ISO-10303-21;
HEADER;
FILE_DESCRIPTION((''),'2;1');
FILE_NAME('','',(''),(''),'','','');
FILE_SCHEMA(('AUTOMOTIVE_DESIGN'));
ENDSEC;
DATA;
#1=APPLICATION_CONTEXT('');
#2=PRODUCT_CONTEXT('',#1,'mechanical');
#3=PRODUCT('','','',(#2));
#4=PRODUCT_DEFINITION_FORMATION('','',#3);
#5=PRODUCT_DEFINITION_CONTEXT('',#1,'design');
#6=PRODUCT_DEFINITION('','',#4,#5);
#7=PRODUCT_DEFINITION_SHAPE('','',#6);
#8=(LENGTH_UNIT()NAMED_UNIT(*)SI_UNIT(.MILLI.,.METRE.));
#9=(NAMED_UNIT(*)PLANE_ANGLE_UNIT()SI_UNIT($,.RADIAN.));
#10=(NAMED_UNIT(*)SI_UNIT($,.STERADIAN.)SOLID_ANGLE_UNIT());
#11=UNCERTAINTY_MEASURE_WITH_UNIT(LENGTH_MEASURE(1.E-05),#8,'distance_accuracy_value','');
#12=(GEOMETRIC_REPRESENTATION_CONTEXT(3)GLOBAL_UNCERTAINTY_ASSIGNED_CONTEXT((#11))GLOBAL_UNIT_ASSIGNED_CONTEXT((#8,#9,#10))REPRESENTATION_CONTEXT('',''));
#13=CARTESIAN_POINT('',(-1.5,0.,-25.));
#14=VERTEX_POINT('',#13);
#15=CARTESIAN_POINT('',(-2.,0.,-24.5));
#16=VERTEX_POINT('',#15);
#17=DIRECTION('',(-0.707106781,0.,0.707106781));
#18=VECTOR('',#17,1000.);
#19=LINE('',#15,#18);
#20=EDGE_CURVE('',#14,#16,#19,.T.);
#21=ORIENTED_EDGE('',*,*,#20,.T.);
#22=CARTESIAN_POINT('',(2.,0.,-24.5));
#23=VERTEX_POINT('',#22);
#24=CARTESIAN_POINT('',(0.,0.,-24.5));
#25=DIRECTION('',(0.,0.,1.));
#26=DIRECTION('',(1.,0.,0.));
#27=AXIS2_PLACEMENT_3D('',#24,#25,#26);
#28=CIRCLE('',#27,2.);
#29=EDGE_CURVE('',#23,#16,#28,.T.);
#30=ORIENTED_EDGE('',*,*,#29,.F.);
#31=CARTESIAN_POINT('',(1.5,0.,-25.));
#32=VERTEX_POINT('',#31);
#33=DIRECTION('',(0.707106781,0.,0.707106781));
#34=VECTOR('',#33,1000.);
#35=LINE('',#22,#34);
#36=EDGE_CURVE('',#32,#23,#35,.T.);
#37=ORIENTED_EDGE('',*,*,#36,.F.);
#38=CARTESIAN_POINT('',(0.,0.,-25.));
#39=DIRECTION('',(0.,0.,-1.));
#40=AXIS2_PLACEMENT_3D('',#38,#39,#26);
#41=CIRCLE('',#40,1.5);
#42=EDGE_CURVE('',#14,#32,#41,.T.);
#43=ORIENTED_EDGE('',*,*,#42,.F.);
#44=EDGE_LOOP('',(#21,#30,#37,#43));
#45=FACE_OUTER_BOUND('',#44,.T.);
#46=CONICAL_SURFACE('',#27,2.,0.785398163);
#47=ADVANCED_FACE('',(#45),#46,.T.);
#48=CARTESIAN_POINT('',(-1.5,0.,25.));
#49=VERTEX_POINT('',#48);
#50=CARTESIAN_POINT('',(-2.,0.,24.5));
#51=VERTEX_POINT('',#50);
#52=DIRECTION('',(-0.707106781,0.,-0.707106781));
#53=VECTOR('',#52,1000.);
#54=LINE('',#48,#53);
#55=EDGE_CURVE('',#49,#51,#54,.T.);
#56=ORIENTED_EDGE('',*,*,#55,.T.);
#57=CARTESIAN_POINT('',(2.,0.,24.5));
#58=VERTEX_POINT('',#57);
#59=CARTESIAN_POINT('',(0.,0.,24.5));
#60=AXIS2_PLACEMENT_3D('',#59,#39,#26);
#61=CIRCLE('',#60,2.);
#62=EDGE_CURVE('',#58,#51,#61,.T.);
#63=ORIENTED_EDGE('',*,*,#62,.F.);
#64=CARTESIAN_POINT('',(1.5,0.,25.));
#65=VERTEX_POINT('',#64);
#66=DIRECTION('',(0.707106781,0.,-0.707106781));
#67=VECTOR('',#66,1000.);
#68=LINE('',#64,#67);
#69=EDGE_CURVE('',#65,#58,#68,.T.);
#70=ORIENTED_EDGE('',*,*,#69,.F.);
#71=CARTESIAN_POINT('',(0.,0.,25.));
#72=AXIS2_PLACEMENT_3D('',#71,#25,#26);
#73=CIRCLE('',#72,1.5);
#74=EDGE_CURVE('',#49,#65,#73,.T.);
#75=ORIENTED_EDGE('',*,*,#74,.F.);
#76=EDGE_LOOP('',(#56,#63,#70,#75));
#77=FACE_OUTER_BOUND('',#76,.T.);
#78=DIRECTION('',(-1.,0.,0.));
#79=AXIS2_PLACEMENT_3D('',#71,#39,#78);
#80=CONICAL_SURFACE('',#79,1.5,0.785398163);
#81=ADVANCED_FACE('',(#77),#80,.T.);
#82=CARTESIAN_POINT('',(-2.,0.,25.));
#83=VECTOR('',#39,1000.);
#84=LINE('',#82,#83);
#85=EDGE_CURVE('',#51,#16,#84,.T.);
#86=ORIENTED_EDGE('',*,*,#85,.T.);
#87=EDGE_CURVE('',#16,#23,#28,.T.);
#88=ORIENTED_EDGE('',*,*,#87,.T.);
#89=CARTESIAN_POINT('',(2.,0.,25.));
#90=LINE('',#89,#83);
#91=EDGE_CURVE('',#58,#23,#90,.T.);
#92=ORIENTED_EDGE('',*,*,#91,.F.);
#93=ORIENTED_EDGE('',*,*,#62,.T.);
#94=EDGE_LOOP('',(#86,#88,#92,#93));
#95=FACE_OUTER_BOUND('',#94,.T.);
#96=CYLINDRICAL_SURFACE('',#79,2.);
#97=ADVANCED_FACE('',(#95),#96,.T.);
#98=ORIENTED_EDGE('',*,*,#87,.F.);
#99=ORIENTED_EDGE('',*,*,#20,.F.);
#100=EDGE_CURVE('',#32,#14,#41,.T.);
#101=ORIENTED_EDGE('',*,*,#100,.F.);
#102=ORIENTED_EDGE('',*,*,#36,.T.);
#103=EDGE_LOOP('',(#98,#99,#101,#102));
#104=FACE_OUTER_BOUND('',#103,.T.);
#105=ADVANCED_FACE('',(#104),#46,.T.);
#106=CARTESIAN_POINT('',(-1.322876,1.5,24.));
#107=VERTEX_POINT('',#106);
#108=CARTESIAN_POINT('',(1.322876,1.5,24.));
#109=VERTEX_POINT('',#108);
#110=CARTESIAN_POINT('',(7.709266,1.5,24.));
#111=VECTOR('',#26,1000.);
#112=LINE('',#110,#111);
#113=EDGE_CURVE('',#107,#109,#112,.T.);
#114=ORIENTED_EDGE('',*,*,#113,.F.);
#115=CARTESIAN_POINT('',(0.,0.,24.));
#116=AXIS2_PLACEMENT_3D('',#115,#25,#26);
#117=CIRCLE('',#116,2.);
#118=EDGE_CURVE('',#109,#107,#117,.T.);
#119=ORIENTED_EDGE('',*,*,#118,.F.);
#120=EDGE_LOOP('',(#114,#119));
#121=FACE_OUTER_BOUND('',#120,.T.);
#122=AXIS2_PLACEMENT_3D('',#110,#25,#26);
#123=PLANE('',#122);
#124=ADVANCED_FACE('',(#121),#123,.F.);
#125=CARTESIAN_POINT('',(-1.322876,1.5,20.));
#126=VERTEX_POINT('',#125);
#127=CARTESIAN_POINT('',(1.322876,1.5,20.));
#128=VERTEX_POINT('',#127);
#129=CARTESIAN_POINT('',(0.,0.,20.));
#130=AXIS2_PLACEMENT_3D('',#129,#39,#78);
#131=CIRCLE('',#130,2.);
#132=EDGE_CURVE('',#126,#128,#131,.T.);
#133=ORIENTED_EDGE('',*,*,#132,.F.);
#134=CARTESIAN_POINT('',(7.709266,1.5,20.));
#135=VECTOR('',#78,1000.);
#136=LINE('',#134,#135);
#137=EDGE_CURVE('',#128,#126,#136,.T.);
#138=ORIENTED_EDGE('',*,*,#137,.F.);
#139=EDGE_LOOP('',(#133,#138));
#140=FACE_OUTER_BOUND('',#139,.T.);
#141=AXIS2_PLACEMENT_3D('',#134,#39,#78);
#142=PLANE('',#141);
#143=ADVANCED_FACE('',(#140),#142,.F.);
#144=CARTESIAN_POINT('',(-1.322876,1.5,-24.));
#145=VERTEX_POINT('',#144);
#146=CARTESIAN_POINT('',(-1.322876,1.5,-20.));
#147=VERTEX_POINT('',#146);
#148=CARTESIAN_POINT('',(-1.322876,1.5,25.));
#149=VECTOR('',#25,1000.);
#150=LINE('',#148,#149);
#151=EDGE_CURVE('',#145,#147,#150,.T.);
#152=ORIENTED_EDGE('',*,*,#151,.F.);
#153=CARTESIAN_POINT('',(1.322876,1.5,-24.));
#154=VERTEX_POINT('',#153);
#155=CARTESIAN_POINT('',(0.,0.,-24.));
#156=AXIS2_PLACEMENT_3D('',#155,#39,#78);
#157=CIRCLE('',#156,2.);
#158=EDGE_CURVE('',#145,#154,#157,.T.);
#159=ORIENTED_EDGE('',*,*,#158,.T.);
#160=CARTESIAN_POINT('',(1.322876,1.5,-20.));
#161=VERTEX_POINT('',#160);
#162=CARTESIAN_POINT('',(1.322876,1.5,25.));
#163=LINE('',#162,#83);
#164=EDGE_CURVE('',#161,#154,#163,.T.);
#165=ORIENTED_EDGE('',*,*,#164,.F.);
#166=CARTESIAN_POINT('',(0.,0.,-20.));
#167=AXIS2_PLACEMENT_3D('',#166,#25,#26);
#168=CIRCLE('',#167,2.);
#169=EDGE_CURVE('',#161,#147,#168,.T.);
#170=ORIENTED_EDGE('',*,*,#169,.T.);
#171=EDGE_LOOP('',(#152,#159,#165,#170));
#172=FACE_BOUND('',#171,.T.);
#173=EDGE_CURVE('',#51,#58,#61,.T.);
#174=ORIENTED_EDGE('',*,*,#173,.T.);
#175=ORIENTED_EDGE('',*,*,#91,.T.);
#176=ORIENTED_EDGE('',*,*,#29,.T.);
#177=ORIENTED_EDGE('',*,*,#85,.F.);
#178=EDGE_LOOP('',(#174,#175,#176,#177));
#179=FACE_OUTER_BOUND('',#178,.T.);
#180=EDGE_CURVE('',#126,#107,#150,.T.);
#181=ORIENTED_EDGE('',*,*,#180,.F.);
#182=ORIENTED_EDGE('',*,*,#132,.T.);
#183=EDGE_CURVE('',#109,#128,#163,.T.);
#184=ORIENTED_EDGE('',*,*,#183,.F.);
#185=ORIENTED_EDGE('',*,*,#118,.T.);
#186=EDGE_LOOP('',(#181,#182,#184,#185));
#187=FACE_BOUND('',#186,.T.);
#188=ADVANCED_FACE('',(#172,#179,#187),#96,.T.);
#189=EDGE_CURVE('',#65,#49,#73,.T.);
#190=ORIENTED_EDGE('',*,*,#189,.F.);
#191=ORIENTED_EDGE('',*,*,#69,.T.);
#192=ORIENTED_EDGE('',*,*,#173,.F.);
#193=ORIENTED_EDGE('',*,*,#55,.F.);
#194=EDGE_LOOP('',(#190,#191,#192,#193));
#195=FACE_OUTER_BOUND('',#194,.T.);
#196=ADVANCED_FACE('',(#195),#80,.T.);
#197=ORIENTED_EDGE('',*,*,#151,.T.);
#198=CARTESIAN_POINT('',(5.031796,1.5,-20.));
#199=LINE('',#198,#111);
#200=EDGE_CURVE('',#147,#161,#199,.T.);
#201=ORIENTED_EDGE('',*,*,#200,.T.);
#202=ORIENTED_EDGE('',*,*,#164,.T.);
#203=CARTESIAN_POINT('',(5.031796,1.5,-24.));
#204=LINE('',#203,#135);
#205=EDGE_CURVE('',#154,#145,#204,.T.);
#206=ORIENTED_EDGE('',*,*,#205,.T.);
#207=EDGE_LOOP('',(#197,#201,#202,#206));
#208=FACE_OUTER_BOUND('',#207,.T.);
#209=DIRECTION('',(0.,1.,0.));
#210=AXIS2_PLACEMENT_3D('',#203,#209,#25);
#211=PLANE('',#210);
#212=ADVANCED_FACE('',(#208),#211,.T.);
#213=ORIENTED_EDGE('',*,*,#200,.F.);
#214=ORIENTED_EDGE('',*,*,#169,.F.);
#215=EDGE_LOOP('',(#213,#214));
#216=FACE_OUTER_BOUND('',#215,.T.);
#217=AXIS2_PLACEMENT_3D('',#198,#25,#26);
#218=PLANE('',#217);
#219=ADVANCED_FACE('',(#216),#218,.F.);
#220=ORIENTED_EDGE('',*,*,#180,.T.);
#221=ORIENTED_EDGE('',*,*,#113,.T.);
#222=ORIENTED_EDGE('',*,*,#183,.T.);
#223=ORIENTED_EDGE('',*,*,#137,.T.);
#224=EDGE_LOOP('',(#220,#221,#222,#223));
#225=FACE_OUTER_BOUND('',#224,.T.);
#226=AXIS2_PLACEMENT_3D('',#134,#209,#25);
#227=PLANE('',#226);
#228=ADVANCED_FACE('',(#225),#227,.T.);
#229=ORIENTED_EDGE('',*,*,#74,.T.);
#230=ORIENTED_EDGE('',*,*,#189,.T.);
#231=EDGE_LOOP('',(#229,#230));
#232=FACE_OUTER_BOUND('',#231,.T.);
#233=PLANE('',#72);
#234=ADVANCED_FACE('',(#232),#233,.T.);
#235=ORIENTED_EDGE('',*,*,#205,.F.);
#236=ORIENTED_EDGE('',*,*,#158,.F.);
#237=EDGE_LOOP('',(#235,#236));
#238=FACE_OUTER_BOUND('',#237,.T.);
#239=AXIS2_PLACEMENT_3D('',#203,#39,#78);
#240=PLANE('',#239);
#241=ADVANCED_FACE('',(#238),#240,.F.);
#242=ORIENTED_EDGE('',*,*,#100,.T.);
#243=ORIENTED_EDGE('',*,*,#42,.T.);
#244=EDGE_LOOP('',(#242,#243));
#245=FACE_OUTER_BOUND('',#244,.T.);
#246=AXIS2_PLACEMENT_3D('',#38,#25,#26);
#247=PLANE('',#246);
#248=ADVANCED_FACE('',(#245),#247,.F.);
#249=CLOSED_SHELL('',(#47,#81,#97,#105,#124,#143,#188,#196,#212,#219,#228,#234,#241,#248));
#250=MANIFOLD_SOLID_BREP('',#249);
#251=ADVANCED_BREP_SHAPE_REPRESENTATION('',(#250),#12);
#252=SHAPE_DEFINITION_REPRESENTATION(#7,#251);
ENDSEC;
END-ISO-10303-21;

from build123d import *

# Parameters (mm, degrees)
SKETCH1_R           = 2
BOSS_EXTRUDE1_DEPTH = 25
SKETCH2_W           = 15.41853157
SKETCH2_H           = 4
SKETCH2_W_2         = 11.817796653
CUT_EXTRUDE1_DEPTH  = 0.5
CHAMFER1_SIZE       = 0.5


with BuildPart() as part:
    # Sketch1 → Boss-Extrude1 (new, symmetric)
    with BuildSketch(Plane.XY):
        Circle(SKETCH1_R)
    extrude(amount=BOSS_EXTRUDE1_DEPTH, both=True)

    # Sketch2 → Cut-Extrude1 (cut)
    with BuildSketch(Plane(origin=(0, 2, 0), x_dir=(-1, 0, 0), z_dir=(0, 1, 0))):
        with Locations((0, 22)):
            Rectangle(SKETCH2_W, SKETCH2_H)
        with Locations((0.877102096, -22)):
            Rectangle(SKETCH2_W_2, SKETCH2_H)
    extrude(amount=-CUT_EXTRUDE1_DEPTH, mode=Mode.SUBTRACT)

    # Chamfer1
    chamfer1_edges = [part.edges().sort_by_distance(p)[0] for p in [
        (-2, 0, -25),
        (-2, 0, 25),
    ]]
    chamfer(chamfer1_edges, length=CHAMFER1_SIZE)


solid = part.part
